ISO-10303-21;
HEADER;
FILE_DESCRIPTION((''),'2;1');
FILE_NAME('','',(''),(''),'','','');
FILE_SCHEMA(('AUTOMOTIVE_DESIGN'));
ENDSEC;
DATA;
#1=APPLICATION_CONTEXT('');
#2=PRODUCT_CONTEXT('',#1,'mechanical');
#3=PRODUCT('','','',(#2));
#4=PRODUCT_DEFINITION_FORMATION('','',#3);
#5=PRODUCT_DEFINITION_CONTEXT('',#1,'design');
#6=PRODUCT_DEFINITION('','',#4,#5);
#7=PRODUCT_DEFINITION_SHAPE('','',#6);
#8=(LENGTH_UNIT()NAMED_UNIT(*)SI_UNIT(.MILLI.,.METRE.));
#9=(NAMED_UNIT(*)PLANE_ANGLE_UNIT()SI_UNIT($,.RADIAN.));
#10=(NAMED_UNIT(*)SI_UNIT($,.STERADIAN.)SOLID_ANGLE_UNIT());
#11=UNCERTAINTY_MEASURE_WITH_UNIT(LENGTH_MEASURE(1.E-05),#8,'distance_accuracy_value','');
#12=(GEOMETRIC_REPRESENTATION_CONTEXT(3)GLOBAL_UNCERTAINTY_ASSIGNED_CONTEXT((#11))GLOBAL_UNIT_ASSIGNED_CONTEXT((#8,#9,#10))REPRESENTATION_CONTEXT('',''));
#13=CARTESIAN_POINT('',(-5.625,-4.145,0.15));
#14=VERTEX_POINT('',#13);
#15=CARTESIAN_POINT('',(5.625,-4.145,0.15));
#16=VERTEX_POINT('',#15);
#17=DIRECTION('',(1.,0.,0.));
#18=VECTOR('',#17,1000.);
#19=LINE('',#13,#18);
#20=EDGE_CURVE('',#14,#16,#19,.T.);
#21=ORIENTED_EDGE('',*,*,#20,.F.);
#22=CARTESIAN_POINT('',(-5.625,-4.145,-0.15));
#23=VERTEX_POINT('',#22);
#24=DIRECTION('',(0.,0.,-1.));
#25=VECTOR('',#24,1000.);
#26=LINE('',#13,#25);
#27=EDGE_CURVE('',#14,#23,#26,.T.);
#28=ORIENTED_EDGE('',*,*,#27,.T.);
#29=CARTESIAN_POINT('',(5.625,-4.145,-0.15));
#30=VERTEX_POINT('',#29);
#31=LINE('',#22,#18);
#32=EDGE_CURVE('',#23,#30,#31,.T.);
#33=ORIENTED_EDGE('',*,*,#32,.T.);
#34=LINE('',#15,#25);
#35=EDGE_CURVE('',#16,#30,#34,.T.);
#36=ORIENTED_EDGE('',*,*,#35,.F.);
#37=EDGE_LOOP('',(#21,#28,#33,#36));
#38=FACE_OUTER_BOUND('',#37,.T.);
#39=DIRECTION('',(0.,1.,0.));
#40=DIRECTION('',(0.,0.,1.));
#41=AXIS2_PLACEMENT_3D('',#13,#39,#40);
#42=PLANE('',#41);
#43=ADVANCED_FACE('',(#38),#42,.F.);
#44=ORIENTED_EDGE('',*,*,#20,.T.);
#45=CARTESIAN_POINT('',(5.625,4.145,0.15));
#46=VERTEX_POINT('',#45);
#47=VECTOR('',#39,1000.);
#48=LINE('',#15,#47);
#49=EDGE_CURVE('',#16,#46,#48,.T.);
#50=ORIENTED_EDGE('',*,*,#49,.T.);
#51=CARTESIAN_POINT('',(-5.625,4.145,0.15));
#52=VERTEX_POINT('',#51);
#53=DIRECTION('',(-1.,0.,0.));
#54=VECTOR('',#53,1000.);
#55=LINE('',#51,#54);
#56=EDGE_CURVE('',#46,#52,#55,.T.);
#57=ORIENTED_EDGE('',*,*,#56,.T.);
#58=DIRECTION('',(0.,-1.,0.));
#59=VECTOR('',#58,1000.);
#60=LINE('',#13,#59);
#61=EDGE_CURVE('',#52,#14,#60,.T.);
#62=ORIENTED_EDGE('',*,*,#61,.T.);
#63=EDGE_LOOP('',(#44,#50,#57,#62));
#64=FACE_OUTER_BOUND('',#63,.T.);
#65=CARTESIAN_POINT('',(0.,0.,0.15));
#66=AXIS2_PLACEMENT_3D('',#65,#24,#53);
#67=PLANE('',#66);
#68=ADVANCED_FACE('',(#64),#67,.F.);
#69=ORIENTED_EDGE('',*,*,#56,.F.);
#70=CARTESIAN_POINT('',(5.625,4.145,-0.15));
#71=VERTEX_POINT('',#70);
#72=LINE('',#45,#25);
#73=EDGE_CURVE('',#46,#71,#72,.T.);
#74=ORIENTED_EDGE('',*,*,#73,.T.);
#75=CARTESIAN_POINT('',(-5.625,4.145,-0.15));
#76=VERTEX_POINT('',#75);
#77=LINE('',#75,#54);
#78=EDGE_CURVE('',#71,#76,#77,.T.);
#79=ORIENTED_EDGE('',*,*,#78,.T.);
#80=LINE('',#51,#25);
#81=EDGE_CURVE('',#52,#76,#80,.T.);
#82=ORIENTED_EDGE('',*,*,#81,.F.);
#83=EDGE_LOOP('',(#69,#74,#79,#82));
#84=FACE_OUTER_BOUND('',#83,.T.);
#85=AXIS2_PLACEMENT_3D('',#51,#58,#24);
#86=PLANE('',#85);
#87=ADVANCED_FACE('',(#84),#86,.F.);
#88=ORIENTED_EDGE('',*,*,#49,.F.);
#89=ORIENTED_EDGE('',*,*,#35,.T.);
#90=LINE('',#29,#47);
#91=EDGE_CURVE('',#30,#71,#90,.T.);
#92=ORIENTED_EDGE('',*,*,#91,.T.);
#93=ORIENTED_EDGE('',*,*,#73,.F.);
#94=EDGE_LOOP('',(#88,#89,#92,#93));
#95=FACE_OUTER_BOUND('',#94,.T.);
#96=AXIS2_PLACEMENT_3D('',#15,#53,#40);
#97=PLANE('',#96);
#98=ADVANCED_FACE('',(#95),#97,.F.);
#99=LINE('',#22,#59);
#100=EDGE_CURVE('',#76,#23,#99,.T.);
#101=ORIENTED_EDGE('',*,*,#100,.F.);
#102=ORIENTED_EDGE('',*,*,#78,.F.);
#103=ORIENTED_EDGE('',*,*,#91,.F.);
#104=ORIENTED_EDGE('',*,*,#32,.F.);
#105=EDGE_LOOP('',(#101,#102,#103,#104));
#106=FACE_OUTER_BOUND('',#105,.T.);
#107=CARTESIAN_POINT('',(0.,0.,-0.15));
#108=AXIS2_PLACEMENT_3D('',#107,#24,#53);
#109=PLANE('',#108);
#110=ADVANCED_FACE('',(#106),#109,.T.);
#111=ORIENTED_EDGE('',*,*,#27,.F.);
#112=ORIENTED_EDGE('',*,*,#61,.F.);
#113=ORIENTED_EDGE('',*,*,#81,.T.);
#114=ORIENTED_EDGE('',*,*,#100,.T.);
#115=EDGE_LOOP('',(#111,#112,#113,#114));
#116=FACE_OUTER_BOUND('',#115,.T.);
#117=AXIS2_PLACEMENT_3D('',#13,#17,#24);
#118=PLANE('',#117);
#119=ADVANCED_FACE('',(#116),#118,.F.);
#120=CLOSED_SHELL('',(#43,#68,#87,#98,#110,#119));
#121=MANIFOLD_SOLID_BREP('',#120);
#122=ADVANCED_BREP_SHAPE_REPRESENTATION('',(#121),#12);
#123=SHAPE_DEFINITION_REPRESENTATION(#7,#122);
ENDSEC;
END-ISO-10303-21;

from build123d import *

# Parameters (mm, degrees)
SKETCH1_W           = 11.25
SKETCH1_H           = 8.29
BOSS_EXTRUDE1_DEPTH = 0.15


with BuildPart() as part:
    # Sketch1 → Boss-Extrude1 (new, symmetric)
    with BuildSketch(Plane.XY):
        Rectangle(SKETCH1_W, SKETCH1_H)
    extrude(amount=BOSS_EXTRUDE1_DEPTH, both=True)


solid = part.part
